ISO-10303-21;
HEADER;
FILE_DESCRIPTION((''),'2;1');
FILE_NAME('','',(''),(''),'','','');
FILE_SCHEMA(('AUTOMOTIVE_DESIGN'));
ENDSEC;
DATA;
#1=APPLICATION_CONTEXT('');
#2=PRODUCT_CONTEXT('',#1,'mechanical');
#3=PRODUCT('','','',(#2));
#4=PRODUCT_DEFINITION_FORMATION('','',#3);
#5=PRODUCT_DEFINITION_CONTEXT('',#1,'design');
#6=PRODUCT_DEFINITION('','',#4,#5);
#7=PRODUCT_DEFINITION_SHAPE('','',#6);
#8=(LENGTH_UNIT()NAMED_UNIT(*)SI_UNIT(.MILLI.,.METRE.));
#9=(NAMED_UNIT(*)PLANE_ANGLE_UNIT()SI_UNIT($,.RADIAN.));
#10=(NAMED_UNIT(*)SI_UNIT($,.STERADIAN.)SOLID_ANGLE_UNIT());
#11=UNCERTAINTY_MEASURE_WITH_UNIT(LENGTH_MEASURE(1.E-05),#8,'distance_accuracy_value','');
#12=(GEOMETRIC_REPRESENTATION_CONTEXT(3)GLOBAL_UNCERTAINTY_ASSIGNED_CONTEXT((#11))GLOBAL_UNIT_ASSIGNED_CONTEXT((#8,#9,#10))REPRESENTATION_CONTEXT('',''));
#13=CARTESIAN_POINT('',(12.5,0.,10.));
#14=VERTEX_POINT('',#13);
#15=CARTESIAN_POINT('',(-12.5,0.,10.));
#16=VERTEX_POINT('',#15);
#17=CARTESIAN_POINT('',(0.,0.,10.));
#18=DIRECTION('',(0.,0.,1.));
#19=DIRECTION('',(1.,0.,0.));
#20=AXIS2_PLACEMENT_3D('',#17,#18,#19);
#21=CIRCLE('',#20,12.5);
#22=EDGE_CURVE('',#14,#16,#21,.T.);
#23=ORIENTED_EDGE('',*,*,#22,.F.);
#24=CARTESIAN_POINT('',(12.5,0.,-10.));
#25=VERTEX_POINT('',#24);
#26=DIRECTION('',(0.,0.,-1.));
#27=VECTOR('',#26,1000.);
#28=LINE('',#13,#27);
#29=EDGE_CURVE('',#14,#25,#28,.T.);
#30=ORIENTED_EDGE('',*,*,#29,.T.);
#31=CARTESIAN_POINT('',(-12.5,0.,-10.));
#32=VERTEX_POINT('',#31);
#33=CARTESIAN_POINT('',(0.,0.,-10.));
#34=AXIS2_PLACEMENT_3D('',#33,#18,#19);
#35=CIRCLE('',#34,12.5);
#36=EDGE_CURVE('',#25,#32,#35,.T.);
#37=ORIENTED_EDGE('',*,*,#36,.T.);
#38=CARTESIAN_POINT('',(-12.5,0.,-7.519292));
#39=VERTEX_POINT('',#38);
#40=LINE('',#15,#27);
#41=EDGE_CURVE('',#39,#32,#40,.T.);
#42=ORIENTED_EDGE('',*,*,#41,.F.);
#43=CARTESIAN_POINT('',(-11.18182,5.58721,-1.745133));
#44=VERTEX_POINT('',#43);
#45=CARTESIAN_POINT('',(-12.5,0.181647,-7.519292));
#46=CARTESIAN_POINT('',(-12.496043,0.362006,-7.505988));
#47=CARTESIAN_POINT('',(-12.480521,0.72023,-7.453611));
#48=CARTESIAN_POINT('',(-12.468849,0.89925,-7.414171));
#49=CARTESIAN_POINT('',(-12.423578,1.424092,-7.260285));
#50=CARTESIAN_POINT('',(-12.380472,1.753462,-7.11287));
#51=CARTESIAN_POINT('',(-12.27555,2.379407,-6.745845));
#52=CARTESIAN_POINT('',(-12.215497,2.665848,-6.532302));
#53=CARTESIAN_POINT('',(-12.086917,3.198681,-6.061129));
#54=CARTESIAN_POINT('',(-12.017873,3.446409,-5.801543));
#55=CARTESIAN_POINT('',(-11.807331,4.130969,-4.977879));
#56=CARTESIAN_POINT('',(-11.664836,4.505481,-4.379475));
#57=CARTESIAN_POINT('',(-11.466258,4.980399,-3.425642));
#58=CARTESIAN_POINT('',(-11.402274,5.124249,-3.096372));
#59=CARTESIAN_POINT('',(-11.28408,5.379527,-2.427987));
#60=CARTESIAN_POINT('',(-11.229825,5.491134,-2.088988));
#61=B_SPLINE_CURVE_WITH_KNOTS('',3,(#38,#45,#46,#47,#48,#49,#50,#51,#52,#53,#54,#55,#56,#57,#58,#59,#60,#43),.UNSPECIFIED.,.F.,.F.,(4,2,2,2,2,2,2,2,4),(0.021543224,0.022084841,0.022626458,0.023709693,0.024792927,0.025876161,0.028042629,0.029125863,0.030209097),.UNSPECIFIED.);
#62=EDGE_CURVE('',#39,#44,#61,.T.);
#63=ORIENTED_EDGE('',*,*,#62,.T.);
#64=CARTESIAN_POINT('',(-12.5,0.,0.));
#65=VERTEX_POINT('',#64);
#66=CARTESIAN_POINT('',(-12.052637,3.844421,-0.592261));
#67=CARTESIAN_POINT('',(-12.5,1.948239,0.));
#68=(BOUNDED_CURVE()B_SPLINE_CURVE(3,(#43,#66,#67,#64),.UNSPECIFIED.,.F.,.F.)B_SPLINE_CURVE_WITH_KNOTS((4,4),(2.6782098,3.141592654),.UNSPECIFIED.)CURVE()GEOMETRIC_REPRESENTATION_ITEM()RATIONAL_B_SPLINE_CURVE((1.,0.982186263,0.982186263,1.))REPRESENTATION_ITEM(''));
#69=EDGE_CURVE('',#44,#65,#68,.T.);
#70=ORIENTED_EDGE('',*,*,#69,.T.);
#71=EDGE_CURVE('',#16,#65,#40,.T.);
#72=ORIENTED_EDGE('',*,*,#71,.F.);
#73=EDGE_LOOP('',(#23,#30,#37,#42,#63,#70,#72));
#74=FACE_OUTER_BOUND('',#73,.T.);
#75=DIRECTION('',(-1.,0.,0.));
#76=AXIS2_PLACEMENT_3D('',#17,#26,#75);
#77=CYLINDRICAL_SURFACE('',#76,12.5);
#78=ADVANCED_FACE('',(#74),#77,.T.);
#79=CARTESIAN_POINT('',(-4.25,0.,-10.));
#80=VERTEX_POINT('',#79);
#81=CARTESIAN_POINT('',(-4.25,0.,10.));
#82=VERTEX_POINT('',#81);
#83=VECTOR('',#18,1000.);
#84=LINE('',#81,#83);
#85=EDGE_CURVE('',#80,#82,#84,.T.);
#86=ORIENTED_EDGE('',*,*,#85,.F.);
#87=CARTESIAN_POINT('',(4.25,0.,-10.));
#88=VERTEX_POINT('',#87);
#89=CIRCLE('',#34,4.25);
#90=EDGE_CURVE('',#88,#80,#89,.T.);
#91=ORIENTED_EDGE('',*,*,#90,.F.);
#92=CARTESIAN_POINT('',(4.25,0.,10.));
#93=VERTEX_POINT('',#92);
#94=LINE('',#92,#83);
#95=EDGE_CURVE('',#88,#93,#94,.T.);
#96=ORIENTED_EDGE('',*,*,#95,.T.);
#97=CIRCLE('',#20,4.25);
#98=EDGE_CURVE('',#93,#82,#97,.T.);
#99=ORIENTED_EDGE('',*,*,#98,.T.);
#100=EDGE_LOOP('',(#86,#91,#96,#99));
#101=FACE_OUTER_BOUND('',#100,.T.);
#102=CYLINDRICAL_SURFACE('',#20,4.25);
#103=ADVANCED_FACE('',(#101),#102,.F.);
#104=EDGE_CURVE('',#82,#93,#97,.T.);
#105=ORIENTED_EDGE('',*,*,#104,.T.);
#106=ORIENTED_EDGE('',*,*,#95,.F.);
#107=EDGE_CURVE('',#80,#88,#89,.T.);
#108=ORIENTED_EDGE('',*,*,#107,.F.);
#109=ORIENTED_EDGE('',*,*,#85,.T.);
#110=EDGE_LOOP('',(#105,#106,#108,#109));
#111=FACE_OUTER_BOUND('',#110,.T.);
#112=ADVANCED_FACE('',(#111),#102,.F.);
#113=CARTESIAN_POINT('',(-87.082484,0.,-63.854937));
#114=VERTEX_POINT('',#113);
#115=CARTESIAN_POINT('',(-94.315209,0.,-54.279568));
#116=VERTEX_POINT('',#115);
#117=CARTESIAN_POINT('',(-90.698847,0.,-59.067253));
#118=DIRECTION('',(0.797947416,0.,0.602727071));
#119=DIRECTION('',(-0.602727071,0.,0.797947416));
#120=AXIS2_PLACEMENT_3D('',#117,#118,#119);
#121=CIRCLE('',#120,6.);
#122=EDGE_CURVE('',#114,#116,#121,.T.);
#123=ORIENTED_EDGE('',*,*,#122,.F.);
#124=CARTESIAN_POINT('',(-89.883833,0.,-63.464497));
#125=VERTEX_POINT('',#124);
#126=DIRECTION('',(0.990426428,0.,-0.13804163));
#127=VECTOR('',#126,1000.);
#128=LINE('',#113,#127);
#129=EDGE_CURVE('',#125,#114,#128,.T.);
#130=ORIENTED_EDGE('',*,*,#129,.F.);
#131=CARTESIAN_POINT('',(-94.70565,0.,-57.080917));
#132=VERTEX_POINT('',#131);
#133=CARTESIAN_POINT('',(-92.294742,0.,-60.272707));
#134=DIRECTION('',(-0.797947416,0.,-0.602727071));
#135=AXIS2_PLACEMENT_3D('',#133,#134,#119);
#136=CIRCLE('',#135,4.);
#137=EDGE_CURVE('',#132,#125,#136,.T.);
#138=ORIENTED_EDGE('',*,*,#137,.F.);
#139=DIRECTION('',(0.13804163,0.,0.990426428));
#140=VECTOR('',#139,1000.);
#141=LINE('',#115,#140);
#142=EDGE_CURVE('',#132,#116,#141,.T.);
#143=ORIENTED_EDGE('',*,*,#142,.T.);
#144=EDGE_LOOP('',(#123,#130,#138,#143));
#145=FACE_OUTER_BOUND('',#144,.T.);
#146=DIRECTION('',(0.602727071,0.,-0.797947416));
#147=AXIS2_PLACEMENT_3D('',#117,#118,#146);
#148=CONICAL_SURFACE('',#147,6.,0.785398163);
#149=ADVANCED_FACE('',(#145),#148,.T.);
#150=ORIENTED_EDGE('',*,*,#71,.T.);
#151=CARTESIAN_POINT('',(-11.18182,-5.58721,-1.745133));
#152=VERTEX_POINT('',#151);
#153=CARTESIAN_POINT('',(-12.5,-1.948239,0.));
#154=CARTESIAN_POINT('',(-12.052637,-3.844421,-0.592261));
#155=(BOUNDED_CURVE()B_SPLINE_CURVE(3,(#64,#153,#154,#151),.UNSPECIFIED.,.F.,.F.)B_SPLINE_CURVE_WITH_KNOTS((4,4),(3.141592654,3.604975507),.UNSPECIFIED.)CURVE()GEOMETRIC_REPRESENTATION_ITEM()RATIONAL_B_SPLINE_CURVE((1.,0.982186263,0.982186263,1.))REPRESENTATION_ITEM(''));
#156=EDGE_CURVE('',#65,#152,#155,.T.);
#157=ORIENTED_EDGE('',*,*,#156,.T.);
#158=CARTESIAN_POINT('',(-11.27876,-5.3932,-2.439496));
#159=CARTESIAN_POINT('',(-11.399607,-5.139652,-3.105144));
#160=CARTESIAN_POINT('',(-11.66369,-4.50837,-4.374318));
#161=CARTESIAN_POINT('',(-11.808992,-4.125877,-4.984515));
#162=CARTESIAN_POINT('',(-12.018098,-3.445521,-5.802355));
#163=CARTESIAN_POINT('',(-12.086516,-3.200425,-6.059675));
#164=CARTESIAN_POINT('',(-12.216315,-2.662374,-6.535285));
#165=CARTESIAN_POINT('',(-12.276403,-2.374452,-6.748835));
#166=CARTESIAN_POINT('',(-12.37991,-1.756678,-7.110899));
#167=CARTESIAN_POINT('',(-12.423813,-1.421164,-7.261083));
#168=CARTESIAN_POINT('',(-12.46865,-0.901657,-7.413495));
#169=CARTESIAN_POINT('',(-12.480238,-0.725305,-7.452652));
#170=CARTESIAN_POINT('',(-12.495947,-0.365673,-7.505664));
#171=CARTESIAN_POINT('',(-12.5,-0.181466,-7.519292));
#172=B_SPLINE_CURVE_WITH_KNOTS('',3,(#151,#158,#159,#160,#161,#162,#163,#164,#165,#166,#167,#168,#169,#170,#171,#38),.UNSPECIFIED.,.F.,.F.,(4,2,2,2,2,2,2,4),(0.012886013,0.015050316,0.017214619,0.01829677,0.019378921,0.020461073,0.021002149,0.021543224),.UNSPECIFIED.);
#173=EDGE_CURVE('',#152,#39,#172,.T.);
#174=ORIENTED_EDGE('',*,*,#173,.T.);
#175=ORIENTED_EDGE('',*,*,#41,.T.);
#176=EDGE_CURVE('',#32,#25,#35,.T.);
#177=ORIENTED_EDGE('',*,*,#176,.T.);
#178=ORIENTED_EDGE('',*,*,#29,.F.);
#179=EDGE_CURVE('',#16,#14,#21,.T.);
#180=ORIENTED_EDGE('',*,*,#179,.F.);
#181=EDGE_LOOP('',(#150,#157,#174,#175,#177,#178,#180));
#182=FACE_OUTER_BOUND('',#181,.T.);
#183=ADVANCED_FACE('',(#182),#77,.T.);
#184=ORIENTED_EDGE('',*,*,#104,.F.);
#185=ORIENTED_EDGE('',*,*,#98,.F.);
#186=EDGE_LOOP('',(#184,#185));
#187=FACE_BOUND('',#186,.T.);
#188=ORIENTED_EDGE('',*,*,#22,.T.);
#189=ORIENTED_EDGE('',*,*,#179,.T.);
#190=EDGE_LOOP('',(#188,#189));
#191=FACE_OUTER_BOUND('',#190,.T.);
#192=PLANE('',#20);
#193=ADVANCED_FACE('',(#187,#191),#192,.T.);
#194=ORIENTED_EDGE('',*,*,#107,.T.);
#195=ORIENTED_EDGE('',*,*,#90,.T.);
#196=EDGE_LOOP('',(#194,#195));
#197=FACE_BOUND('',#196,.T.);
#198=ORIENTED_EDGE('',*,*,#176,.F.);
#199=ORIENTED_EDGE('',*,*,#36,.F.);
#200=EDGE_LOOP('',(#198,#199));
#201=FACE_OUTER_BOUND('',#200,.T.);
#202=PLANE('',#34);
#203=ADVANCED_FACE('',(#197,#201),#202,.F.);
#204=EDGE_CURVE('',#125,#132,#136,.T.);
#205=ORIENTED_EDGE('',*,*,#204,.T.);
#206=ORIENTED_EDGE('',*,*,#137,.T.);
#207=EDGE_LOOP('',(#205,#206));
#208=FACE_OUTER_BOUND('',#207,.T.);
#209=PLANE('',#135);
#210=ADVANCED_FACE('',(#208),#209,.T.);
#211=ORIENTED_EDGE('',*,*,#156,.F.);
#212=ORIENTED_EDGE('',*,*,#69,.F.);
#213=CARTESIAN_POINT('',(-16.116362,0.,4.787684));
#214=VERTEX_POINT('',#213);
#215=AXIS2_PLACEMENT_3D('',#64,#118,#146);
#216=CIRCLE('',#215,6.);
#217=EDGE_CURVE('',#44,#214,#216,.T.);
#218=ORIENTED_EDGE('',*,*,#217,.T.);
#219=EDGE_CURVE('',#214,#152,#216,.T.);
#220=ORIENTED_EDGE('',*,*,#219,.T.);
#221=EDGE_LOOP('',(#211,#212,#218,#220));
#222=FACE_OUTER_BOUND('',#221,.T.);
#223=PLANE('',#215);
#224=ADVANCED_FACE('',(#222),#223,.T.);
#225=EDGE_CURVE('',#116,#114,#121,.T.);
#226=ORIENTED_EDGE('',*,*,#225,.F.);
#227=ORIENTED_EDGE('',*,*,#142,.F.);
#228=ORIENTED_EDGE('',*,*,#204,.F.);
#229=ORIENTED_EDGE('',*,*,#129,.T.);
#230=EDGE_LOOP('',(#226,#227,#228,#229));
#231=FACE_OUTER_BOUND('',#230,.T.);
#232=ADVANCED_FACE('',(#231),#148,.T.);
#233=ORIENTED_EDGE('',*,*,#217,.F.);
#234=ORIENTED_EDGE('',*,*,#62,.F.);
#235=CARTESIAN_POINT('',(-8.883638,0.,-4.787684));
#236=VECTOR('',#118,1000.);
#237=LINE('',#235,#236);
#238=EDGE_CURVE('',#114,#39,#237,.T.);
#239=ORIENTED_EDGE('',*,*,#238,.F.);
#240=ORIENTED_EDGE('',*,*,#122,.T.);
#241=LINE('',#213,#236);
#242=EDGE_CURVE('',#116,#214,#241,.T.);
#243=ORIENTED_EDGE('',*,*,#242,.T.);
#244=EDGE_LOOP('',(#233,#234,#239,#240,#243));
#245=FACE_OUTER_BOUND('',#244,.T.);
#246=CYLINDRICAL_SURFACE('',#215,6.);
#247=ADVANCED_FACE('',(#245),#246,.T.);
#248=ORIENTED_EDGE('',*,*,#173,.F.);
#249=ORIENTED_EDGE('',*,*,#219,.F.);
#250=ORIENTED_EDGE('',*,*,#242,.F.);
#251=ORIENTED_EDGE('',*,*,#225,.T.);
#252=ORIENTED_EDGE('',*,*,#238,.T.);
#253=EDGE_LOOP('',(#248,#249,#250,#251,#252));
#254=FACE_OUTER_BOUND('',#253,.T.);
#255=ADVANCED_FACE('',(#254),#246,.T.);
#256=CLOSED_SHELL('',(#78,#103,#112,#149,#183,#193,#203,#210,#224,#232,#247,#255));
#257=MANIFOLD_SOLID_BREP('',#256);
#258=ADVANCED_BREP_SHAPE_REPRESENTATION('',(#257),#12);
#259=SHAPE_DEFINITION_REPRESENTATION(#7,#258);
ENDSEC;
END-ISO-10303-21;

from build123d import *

# Parameters (mm, degrees)
SKETCH1_R           = 12.5
BOSS_EXTRUDE1_DEPTH = 10
M10_TAPPED_HOLE1_D  = 8.5
CHAMFER1_SIZE       = 2


with BuildPart() as part:
    # Sketch1 → Boss-Extrude1 (new, symmetric)
    with BuildSketch(Plane.XY):
        Circle(SKETCH1_R)
    extrude(amount=BOSS_EXTRUDE1_DEPTH, both=True)

    # M10 Tapped Hole1 (through all)
    with Locations(Plane.XY.offset(10)):
        with Locations((0, 0)):
            Hole(M10_TAPPED_HOLE1_D / 2)

    # Sketch5 → Revolve1 (revolve)
    with BuildSketch(Plane(origin=(0, 0, 0), x_dir=(1, 0, 0), z_dir=(0, 1, 0))):
        Polygon((-12.5, 0), (-92.29474156, 60.272707085), (-88.678379135, 65.060391578), (-8.883637575, 4.787684494), align=None)
    revolve(axis=Axis((-12.5, 0, 0), (-0.7979474156035873, 0, -0.6027270708467937)))

    # Chamfer1
    chamfer1_edges = [part.edges().sort_by_distance(p)[0] for p in [
        (-95.911103985, 0, -55.485022591),
    ]]
    chamfer(chamfer1_edges, length=CHAMFER1_SIZE)


solid = part.part
